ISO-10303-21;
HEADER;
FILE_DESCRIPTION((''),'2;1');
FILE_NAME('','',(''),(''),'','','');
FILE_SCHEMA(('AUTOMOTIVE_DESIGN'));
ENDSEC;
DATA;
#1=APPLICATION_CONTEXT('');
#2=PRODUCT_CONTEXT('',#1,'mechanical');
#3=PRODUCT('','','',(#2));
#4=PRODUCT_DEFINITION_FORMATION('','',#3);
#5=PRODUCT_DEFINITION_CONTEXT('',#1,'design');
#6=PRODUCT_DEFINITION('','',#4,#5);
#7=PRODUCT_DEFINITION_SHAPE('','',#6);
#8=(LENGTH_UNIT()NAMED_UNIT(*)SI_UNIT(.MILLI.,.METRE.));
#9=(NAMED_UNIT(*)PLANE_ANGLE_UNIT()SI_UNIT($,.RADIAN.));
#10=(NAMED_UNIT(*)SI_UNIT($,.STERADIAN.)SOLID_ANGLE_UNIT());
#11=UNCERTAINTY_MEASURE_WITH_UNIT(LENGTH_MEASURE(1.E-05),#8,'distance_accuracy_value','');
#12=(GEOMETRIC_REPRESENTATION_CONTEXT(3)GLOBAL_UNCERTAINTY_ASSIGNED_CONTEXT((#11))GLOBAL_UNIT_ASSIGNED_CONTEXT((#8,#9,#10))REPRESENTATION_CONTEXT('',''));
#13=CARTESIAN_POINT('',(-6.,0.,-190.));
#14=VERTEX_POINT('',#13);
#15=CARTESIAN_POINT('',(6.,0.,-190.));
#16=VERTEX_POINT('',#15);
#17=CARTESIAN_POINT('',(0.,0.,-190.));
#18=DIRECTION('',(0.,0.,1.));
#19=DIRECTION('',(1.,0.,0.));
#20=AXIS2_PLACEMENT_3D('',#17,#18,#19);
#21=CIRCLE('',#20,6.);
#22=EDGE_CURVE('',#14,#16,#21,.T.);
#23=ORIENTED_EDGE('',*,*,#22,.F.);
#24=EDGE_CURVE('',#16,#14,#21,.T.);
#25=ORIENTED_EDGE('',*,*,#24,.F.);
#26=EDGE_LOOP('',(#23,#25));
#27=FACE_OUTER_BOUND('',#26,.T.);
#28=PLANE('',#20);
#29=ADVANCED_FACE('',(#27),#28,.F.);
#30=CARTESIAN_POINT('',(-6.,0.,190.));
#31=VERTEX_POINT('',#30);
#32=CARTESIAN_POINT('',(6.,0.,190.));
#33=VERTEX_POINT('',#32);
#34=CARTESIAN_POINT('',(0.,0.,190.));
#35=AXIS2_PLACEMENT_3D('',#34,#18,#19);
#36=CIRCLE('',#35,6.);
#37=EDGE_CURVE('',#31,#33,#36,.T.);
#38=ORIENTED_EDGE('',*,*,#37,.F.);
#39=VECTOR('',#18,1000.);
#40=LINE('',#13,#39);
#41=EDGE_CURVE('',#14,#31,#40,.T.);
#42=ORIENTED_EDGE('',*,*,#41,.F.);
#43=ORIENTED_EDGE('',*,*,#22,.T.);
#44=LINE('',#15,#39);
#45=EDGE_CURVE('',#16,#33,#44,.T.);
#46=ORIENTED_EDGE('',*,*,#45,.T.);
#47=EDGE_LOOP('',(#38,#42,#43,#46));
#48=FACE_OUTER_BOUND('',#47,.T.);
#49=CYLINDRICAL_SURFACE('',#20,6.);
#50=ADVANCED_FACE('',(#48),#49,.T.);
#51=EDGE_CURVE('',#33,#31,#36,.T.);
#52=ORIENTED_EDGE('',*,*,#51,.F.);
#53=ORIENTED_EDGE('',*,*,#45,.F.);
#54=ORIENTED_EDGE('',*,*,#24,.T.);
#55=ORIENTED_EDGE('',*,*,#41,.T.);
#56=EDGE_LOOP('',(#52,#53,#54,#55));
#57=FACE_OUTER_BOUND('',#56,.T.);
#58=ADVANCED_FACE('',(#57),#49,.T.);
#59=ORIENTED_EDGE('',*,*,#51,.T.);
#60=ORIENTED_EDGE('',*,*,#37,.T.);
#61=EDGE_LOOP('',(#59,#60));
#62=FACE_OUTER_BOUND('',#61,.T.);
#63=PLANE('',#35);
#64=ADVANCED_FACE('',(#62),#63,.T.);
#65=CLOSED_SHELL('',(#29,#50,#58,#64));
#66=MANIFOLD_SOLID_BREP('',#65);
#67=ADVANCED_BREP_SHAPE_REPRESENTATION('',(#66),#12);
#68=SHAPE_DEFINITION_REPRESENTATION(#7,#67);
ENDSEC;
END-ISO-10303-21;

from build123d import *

# Parameters (mm, degrees)
SKETCH_1_R      = 6
EXTRUDE_1_DEPTH = 190


with BuildPart() as part:
    # 草图1 → 凸台-拉伸1 (new, symmetric)
    with BuildSketch(Plane.XY):
        Circle(SKETCH_1_R)
    extrude(amount=EXTRUDE_1_DEPTH, both=True)


solid = part.part
